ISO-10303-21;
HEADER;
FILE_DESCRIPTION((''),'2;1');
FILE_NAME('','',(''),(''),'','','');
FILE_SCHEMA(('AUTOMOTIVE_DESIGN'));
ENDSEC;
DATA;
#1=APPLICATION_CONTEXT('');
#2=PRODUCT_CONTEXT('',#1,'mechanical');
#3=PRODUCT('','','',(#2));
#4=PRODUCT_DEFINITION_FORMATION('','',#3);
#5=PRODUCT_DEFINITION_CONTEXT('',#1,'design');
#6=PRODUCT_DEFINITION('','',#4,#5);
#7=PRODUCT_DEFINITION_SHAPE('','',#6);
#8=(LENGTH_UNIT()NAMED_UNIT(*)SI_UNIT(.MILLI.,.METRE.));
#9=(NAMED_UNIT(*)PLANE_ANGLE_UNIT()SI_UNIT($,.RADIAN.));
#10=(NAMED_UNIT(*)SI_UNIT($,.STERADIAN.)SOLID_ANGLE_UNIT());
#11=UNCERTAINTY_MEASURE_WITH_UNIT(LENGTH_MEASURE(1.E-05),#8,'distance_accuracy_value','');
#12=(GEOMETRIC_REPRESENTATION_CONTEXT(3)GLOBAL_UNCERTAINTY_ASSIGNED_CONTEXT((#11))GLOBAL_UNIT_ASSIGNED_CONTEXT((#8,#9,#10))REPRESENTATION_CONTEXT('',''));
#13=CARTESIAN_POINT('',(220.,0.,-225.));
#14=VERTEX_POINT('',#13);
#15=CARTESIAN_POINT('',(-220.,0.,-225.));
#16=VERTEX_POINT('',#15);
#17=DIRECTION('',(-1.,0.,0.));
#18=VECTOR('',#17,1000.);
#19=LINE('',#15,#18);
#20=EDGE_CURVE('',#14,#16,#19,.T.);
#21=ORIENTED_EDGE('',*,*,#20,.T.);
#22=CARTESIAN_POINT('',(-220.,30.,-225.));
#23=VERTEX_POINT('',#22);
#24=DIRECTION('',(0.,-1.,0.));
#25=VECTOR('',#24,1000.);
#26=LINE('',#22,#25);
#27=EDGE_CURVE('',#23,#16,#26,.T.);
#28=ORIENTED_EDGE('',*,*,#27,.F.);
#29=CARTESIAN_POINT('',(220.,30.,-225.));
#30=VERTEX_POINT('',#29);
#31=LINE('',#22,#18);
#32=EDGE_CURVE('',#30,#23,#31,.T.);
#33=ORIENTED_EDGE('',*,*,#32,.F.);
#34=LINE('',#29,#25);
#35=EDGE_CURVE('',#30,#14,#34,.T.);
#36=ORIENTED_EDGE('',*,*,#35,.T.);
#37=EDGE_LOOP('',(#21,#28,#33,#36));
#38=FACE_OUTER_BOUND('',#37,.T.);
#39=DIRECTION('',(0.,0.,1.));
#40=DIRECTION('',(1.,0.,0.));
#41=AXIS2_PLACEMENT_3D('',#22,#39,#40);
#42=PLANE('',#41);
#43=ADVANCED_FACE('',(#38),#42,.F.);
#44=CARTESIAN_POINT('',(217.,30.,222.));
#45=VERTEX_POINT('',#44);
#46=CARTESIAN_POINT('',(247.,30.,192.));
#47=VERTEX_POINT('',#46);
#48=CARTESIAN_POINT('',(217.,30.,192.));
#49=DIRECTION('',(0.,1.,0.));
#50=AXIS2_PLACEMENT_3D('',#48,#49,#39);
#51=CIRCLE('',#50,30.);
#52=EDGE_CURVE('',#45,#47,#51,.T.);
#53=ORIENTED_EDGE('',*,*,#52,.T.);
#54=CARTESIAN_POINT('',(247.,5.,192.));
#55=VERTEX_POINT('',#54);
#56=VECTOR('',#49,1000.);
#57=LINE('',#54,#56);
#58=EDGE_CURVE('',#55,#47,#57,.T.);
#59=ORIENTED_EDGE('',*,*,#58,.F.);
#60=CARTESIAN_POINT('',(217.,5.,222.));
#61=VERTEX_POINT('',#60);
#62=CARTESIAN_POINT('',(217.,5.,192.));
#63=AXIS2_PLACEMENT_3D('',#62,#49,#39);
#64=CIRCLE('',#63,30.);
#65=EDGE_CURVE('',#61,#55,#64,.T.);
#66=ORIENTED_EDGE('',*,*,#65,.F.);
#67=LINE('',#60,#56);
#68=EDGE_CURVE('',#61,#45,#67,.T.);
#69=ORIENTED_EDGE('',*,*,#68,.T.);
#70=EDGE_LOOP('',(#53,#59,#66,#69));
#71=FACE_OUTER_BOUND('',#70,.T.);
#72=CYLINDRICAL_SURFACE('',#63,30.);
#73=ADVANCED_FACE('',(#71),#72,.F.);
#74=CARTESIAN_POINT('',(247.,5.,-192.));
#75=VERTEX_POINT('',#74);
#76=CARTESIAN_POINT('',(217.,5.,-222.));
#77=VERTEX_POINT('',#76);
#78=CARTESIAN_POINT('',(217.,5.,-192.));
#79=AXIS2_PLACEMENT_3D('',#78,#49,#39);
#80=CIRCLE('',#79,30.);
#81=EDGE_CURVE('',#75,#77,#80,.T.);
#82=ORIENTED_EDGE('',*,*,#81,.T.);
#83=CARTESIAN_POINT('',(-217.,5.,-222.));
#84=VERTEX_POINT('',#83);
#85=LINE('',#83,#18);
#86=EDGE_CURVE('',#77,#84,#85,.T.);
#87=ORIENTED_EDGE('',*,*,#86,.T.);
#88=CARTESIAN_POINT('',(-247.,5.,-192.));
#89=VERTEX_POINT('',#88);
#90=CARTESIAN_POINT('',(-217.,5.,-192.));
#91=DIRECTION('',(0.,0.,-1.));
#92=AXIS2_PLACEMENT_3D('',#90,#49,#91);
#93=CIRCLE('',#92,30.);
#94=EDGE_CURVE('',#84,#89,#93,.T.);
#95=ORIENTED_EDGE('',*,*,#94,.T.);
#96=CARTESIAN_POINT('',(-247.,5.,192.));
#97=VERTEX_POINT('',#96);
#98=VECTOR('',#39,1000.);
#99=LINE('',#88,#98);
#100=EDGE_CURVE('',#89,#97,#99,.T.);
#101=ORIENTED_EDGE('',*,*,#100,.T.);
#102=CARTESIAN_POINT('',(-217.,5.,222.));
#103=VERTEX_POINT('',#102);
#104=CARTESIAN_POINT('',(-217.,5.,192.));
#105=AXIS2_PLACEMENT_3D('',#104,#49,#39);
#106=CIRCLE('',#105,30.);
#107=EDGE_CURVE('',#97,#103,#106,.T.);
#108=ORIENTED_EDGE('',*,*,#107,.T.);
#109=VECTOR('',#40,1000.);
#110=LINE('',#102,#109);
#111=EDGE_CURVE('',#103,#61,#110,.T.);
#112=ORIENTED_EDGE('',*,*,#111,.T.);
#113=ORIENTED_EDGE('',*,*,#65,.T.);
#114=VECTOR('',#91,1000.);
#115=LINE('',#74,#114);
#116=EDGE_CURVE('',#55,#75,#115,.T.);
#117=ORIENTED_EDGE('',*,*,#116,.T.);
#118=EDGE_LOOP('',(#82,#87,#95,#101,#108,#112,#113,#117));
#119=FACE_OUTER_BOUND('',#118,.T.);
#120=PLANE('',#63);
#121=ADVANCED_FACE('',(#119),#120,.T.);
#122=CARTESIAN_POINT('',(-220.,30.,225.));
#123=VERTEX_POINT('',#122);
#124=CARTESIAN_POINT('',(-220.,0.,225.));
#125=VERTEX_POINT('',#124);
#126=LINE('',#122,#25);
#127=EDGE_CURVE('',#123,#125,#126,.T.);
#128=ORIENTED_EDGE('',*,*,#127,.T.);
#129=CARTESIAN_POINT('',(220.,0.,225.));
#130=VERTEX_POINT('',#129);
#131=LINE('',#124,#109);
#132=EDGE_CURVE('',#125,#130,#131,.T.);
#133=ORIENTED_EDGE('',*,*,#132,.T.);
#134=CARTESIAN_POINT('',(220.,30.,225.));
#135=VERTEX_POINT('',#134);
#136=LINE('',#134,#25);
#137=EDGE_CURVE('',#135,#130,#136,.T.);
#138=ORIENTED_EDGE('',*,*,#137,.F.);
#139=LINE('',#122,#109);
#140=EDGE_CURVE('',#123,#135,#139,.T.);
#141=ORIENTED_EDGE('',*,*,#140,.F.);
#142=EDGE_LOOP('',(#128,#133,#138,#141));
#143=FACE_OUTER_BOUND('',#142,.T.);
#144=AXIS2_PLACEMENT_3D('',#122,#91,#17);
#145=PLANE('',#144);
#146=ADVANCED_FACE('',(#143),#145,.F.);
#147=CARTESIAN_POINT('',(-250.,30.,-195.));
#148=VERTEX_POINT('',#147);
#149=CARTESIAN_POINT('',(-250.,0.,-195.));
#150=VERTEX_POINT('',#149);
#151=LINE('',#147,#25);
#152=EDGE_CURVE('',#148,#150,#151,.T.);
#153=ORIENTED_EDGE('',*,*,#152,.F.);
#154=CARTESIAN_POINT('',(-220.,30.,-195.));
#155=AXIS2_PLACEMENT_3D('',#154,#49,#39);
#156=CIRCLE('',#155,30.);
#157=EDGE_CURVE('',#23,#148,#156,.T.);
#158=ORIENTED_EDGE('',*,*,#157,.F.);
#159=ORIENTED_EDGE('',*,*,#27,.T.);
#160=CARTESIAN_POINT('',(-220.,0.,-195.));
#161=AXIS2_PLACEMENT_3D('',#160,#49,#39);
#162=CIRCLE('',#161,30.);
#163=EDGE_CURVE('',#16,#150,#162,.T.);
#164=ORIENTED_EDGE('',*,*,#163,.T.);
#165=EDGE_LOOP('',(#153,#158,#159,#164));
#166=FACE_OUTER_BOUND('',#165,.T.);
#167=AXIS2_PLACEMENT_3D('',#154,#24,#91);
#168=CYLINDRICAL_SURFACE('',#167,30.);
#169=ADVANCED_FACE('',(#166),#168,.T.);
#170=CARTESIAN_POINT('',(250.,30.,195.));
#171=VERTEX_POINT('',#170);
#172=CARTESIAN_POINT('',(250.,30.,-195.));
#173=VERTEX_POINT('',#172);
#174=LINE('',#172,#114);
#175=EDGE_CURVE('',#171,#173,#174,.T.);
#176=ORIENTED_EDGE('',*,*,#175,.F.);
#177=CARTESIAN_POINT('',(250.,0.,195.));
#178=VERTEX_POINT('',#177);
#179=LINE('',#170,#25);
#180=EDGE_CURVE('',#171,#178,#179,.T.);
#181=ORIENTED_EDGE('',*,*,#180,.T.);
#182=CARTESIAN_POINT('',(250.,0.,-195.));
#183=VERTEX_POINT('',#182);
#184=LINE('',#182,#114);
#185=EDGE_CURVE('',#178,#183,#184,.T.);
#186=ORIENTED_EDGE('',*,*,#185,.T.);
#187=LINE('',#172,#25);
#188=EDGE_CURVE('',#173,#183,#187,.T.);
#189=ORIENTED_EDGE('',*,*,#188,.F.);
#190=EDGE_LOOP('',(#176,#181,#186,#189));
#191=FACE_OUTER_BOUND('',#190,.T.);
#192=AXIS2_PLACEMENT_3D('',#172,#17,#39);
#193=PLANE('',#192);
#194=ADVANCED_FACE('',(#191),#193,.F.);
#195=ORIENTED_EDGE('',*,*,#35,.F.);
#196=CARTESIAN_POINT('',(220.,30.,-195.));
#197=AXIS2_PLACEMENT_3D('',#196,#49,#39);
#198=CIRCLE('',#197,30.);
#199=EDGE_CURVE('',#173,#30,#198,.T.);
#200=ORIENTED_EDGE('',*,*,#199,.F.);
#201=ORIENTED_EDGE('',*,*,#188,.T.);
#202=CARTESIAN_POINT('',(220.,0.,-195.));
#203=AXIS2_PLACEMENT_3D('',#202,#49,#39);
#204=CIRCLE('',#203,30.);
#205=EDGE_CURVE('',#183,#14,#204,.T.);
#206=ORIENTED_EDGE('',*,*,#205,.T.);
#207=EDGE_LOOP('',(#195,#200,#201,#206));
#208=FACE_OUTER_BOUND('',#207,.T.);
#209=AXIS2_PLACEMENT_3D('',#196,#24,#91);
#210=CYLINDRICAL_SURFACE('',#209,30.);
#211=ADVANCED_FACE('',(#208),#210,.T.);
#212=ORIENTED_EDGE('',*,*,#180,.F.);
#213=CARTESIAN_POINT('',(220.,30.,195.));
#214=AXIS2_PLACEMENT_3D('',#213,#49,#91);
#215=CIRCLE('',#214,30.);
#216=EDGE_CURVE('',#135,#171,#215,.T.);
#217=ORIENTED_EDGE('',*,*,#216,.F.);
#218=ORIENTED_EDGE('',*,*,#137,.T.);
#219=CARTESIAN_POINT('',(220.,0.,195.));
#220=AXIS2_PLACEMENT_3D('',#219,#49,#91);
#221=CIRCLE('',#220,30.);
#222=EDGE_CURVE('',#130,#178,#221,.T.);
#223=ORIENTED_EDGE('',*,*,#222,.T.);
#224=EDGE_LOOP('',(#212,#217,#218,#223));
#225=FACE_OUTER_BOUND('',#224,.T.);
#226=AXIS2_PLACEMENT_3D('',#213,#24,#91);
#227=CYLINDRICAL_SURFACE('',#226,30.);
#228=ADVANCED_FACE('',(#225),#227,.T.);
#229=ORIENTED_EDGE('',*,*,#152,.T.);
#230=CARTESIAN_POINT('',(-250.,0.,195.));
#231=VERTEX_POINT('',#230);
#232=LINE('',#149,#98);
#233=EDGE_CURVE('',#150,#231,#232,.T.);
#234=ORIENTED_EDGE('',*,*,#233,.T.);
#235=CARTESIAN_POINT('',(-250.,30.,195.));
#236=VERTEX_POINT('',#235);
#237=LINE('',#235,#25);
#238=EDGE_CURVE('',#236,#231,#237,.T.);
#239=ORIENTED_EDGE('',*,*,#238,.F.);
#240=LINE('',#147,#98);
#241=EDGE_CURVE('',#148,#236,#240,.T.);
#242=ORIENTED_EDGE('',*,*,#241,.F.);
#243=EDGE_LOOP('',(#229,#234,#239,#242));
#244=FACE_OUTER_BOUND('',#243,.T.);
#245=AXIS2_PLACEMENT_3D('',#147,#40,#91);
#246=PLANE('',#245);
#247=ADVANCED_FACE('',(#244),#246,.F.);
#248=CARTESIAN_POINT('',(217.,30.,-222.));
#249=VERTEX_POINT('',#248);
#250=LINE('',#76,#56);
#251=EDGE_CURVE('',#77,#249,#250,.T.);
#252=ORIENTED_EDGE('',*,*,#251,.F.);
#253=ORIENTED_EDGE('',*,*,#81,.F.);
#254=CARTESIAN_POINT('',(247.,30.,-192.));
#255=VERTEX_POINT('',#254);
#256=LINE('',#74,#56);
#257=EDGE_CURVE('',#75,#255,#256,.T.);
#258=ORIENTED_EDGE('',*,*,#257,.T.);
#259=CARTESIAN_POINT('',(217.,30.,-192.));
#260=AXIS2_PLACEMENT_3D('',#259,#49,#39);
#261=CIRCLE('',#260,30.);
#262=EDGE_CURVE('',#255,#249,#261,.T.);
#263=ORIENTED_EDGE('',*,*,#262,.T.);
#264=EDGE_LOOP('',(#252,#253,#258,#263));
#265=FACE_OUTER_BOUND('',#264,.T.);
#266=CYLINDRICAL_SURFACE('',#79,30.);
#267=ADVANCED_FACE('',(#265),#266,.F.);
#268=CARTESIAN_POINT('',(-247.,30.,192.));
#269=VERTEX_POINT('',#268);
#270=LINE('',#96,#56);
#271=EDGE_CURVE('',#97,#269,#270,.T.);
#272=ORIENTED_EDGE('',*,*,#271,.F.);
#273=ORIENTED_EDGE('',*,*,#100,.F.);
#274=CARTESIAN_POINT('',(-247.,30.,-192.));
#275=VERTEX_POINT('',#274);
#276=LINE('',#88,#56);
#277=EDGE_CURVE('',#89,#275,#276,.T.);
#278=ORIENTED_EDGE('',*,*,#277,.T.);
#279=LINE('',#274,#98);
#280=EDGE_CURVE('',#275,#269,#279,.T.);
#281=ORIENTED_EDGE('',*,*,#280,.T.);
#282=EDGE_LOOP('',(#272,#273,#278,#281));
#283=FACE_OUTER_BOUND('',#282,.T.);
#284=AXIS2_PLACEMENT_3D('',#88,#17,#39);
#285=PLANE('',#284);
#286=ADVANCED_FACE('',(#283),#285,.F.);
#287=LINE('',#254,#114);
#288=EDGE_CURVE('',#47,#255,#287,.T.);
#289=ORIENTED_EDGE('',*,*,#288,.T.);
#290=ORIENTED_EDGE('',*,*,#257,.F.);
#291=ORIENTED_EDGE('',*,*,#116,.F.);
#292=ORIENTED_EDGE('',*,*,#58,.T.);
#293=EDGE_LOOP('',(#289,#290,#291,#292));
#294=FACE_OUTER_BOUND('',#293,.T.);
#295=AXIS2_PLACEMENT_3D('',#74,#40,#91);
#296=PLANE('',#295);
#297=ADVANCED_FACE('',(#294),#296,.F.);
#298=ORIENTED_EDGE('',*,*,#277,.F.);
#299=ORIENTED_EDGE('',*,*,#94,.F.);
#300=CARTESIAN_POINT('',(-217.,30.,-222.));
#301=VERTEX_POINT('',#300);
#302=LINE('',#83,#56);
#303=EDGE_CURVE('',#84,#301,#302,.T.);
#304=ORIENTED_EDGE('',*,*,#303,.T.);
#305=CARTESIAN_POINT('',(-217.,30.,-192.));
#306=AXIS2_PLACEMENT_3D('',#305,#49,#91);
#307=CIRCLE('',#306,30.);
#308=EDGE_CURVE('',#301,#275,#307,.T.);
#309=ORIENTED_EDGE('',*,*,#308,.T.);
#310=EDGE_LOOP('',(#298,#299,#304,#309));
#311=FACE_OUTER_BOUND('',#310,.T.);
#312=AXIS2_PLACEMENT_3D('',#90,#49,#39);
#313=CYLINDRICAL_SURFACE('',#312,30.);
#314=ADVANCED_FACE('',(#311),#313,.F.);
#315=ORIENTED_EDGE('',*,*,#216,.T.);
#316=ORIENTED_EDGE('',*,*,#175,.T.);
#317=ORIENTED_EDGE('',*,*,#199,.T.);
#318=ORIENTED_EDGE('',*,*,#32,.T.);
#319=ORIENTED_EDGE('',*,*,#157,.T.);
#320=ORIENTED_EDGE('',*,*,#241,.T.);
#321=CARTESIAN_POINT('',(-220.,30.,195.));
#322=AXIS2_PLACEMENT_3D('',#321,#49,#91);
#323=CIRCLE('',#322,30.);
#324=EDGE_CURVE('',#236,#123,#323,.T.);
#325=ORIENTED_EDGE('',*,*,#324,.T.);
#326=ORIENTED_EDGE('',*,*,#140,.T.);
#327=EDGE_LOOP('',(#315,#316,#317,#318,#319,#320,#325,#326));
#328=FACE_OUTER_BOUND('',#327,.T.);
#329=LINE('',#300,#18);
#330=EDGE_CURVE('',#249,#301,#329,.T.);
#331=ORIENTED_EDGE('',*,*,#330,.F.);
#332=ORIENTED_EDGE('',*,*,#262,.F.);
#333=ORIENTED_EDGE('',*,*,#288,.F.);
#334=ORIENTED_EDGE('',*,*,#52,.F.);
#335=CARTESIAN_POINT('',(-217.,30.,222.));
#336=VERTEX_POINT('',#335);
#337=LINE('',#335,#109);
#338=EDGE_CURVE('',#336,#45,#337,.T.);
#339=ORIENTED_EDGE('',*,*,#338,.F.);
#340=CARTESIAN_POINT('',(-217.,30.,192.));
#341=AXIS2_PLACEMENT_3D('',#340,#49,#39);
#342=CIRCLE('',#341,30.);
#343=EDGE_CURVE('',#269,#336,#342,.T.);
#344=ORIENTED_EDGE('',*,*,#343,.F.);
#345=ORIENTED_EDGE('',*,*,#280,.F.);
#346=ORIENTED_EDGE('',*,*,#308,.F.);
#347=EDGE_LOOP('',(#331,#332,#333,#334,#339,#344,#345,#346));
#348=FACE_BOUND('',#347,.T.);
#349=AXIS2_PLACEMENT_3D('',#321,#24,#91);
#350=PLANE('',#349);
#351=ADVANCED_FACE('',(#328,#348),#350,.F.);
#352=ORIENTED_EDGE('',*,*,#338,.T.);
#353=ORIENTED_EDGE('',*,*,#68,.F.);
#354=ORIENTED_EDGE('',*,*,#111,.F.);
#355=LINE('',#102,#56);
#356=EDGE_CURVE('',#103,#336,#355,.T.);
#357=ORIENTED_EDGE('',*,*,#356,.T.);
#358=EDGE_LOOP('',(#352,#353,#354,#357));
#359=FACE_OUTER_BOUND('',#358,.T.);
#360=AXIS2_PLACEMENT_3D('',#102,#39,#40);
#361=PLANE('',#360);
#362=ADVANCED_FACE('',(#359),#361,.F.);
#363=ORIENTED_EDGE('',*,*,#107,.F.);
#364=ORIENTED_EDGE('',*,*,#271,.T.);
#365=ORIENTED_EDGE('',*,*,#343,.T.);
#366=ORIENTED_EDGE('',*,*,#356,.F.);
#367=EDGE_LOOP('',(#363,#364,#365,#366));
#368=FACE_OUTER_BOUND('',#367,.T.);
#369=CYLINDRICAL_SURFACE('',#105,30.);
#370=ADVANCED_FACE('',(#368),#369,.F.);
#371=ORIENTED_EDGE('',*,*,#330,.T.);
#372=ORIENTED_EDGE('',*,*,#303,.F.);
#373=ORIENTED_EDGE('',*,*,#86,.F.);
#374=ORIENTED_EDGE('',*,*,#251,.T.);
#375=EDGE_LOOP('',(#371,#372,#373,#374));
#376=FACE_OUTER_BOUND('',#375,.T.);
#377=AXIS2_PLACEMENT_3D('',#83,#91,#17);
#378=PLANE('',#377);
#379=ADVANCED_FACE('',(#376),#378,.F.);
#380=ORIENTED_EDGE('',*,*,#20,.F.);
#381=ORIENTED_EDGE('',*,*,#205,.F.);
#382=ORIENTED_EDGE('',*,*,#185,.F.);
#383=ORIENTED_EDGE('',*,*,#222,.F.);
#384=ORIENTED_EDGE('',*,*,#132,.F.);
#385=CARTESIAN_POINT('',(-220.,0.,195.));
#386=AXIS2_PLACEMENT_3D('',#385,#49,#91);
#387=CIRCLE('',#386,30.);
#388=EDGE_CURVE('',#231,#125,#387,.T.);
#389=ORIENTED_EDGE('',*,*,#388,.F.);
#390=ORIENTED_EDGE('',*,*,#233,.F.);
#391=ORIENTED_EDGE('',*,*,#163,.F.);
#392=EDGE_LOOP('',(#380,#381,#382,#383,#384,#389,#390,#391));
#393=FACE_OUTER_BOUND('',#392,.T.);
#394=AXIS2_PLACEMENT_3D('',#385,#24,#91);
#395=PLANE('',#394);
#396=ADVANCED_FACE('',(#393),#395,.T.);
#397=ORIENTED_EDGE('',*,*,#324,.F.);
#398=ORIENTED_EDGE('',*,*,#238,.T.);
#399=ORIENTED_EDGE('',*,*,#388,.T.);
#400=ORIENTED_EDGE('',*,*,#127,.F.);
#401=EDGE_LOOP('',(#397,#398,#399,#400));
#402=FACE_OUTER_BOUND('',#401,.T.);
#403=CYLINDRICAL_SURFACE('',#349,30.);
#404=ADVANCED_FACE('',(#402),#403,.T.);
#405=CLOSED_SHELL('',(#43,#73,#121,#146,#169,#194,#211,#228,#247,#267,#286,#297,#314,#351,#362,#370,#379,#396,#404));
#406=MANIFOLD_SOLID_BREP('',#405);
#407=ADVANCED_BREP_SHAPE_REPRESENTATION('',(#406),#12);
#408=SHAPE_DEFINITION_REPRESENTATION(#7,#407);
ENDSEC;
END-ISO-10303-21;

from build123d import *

# Parameters (mm, degrees)
BOSS_EXTRUDE1_DEPTH = 30
CUT_EXTRUDE1_DEPTH  = 25


with BuildPart() as part:
    # Sketch1 → Boss-Extrude1 (new body)
    with BuildSketch(Plane(origin=(0, 0, 0), x_dir=(1, 0, 0), z_dir=(0, 1, 0))):
        with BuildLine():
            Line((-220, 225), (220, 225))
            ThreePointArc((220, 225), (241.213203436, 216.213203436), (250, 195))
            Line((250, 195), (250, -195))
            ThreePointArc((250, -195), (241.213203436, -216.213203436), (220, -225))
            Line((220, -225), (-220, -225))
            ThreePointArc((-220, -225), (-241.213203436, -216.213203436), (-250, -195))
            Line((-250, -195), (-250, 195))
            ThreePointArc((-250, 195), (-241.213203436, 216.213203436), (-220, 225))
        make_face()
    extrude(amount=BOSS_EXTRUDE1_DEPTH)

    # Sketch2 → Cut-Extrude1 (cut)
    with BuildSketch(Plane(origin=(0, 30, 0), x_dir=(1, 0, 0), z_dir=(0, 1, 0))):
        with BuildLine():
            Line((-217, 222), (217, 222))
            ThreePointArc((217, 222), (238.213203436, 213.213203436), (247, 192))
            Line((247, 192), (247, -192))
            ThreePointArc((247, -192), (238.213203436, -213.213203436), (217, -222))
            Line((217, -222), (-217, -222))
            ThreePointArc((-217, -222), (-238.213203436, -213.213203436), (-247, -192))
            Line((-247, -192), (-247, 192))
            ThreePointArc((-247, 192), (-238.213203436, 213.213203436), (-217, 222))
        make_face()
    extrude(amount=-CUT_EXTRUDE1_DEPTH, mode=Mode.SUBTRACT)


solid = part.part
